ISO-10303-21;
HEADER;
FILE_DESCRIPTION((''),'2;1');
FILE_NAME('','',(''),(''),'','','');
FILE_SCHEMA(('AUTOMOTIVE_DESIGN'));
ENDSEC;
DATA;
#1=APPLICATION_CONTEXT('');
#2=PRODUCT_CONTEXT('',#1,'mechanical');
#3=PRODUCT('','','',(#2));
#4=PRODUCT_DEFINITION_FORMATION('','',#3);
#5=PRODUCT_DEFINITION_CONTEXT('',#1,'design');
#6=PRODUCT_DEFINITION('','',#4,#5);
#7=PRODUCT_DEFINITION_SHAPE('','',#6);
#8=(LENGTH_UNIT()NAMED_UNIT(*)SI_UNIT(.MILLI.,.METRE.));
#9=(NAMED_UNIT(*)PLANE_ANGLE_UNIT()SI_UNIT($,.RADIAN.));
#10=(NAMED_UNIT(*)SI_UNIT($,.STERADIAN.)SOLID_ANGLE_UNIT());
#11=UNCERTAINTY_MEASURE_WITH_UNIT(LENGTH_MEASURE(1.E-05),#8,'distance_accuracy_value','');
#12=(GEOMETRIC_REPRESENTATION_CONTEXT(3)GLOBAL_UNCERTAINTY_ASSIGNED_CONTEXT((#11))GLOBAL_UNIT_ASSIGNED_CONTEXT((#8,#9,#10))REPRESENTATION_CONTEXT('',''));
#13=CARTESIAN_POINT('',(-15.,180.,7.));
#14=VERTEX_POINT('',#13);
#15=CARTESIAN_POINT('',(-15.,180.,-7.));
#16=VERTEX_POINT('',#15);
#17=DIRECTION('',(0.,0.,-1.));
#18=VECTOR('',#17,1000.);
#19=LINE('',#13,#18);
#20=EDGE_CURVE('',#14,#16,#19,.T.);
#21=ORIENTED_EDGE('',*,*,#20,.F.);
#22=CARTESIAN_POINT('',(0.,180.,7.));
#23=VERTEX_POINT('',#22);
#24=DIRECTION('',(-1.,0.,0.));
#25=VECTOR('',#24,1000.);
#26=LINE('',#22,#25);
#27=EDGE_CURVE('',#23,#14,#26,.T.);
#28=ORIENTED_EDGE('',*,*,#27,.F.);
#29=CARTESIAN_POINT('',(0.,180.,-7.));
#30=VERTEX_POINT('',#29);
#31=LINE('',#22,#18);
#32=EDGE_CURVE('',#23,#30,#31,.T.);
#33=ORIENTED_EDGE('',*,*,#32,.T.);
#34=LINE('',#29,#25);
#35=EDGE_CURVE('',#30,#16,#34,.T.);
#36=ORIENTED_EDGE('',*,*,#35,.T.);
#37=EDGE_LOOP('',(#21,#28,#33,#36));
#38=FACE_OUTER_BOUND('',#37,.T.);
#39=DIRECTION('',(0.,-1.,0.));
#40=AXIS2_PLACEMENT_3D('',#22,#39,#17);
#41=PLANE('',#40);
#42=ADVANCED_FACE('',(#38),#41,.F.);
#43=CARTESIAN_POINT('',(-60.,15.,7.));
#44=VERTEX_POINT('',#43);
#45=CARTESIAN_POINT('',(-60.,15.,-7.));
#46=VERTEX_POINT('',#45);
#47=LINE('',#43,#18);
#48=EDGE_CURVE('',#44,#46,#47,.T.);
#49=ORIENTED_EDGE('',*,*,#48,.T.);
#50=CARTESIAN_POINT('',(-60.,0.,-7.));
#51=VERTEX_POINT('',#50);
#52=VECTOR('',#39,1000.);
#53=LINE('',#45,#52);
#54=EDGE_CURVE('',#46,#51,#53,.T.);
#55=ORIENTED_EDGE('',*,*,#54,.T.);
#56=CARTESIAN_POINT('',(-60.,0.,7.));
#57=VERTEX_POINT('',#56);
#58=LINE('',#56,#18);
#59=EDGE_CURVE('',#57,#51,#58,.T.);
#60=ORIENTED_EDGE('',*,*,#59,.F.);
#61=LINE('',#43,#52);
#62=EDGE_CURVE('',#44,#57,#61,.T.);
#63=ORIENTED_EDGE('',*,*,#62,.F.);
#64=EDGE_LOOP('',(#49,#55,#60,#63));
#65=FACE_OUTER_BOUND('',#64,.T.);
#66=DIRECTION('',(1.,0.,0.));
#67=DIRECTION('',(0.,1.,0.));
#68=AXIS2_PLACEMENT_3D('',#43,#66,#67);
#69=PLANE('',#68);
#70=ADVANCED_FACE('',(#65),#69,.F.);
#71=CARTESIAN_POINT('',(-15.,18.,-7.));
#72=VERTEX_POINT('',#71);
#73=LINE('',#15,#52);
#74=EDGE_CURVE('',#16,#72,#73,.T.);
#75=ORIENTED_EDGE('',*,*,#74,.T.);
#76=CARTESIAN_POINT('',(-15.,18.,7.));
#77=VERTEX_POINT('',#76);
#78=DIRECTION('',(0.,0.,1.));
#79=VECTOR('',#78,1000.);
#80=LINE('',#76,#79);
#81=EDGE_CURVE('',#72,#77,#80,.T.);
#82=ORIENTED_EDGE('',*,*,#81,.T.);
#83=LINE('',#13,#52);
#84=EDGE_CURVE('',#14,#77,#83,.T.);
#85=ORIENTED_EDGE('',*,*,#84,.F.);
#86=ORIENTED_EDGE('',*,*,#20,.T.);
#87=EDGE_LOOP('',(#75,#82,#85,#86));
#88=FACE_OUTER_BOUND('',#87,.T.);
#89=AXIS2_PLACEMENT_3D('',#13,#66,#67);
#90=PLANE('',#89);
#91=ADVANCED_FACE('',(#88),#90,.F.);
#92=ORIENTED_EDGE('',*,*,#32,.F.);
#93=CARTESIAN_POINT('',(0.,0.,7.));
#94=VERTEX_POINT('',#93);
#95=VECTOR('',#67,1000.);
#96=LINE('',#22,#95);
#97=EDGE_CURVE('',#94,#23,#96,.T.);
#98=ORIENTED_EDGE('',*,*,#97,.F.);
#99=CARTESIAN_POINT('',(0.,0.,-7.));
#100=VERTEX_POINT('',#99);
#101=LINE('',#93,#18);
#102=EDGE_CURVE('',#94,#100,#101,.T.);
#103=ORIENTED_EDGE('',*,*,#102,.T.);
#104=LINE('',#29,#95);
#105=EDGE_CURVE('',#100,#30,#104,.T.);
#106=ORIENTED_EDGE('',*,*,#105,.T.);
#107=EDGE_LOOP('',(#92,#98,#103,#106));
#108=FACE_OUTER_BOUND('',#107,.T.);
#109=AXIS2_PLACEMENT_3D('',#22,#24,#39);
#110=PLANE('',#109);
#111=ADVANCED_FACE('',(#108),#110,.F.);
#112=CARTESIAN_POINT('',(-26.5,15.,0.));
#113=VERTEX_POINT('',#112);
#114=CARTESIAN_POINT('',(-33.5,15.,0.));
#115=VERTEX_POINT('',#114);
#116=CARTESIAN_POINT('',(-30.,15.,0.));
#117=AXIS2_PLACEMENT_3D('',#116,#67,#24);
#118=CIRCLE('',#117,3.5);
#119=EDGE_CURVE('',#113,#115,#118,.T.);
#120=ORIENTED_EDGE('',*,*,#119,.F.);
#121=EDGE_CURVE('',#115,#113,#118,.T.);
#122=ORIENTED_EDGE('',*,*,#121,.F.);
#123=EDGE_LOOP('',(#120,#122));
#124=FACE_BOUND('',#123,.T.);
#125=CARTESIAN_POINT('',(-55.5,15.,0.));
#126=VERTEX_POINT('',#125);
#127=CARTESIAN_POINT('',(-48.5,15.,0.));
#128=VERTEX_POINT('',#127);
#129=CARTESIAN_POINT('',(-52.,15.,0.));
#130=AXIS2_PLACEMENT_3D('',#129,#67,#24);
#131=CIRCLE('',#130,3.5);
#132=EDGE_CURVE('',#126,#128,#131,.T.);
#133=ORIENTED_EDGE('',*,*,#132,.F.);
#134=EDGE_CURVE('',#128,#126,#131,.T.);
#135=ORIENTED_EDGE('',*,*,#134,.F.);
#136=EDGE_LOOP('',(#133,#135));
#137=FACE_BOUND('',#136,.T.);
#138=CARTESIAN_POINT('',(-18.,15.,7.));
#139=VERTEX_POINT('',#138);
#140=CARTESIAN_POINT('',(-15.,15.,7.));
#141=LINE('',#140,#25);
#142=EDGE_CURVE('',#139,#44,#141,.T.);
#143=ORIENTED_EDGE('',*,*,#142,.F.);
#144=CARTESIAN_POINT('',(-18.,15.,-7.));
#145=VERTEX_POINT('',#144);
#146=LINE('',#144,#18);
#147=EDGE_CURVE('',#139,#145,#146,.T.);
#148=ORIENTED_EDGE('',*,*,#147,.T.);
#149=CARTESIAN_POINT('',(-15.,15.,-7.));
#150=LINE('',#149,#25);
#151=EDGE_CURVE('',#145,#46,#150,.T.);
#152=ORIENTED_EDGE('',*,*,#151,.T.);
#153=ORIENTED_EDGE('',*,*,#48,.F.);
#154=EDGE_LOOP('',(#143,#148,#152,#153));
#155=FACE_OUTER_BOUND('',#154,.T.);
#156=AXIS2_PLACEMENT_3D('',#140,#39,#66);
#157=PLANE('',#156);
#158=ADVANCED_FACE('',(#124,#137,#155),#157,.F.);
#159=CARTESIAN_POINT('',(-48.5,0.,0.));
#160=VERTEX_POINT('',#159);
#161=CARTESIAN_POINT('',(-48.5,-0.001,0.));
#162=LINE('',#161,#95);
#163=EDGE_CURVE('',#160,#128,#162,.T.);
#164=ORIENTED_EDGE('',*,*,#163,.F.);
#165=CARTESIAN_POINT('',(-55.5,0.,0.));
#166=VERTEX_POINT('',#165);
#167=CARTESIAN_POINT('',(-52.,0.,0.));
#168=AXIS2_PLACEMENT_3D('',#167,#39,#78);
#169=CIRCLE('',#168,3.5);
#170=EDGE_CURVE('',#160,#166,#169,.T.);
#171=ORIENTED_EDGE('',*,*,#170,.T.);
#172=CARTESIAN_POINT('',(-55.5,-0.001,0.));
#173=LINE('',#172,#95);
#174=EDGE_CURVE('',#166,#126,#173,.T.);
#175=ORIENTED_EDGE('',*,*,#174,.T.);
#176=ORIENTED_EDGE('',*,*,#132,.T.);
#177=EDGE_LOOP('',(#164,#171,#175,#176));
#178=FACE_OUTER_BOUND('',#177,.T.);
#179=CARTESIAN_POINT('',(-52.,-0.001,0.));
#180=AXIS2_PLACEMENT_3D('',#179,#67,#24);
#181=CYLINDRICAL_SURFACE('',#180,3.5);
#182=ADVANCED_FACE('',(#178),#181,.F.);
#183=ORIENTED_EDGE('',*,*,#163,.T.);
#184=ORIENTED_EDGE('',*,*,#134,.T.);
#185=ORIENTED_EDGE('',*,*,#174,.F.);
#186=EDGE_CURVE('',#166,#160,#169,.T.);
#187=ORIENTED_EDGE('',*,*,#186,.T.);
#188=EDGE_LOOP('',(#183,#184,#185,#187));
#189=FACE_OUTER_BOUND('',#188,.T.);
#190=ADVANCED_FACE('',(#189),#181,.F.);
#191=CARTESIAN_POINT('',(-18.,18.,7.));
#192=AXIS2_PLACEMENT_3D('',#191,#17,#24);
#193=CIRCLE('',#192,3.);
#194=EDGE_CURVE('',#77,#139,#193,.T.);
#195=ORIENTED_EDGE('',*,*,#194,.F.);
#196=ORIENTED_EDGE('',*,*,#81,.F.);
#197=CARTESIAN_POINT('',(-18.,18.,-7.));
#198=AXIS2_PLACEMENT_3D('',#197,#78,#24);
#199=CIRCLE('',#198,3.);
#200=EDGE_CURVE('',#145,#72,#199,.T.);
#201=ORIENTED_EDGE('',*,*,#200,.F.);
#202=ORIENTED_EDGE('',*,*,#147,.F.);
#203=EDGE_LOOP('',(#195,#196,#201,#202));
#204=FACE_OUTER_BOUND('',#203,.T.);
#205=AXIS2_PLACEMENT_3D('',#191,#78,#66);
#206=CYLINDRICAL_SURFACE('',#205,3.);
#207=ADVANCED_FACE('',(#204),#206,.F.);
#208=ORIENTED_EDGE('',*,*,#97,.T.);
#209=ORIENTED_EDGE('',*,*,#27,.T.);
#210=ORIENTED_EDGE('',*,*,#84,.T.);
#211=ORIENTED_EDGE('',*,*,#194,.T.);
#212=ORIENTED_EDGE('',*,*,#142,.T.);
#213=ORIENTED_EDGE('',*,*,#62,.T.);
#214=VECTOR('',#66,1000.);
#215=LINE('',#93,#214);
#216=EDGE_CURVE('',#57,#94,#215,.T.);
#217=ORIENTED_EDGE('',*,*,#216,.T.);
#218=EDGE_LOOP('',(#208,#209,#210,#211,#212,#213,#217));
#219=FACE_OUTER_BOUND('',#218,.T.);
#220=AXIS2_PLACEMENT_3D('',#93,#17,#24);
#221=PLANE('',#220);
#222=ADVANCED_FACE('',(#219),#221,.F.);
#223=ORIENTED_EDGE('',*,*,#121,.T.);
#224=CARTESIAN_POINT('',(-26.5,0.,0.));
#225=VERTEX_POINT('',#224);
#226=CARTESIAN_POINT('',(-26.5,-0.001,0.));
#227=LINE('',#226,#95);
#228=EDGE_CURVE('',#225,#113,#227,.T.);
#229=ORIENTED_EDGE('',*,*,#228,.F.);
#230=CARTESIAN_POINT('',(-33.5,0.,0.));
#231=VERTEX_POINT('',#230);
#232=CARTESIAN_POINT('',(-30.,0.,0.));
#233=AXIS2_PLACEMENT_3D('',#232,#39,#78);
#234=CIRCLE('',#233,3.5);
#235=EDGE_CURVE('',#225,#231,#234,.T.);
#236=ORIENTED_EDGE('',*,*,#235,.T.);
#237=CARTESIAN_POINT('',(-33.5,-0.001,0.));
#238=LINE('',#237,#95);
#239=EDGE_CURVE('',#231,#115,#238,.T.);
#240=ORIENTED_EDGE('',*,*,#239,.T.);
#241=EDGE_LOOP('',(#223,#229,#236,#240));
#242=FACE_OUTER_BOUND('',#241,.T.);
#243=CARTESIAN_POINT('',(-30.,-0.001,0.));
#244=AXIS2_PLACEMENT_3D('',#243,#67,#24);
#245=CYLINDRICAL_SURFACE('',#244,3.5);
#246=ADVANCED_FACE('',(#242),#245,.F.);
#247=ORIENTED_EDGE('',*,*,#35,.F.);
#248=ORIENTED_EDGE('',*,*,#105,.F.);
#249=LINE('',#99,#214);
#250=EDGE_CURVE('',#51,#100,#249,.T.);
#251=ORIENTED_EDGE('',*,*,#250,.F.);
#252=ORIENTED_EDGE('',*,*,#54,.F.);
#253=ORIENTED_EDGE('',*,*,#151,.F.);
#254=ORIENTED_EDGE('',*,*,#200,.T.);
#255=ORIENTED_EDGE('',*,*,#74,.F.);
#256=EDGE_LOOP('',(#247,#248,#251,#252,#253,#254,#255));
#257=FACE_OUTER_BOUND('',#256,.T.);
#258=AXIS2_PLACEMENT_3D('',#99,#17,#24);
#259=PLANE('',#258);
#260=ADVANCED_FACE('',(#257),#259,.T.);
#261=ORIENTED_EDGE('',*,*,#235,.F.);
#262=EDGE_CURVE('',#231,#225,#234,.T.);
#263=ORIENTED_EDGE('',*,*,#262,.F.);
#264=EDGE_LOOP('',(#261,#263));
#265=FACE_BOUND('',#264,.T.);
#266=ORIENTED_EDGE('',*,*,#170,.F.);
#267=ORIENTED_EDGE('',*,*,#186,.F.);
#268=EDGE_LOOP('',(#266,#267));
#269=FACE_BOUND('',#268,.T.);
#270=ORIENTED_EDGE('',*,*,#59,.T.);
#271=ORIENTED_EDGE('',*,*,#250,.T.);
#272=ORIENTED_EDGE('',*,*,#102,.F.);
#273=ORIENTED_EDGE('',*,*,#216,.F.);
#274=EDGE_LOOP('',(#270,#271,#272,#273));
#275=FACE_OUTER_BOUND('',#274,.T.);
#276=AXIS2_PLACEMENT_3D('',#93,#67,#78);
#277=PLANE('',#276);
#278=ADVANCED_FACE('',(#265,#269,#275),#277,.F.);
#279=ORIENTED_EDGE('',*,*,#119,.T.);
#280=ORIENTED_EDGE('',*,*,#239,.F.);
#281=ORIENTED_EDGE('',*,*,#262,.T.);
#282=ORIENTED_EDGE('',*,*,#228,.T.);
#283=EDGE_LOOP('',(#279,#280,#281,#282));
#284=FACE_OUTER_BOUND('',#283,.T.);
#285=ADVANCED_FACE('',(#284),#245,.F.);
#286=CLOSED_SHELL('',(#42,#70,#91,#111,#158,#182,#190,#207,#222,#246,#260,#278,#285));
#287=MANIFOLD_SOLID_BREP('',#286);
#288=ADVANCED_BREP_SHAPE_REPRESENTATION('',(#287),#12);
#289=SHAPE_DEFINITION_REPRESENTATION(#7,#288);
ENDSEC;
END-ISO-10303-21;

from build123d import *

# Parameters (mm, degrees)
EXTRUDE_1_DEPTH     = 7
FILLET_1_R          = 3
CUT_EXTRUDE_1_REACH = 177.71
SKETCH_3_R          = 3.5


with BuildPart() as part:
    # 草图1 → 凸台-拉伸1 (new, symmetric)
    with BuildSketch(Plane.XY):
        Polygon((0, 180), (-15, 180), (-15, 15), (-60, 15), (-60, 0), (0, 0), align=None)
    extrude(amount=EXTRUDE_1_DEPTH, both=True)

    # 圆角1
    fillet_1_edges = [part.edges().sort_by_distance(p)[0] for p in [
        (-15, 15, 0),
    ]]
    fillet(fillet_1_edges, radius=FILLET_1_R)

    # 草图3 → 切除-拉伸1 (cut, up to next)
    with BuildSketch(Plane(origin=(0, 15, 0), x_dir=(1, 0, 0), z_dir=(0, 1, 0)), mode=Mode.PRIVATE) as cut_extrude_1_sk1:
        with Locations(Location((-52, 0, 0), (0, 0, 180))):
            Circle(SKETCH_3_R)
    cut_extrude_1_tool1 = extrude(cut_extrude_1_sk1.sketch, amount=-CUT_EXTRUDE_1_REACH, mode=Mode.PRIVATE) & part.part
    # 草图3 → 切除-拉伸1 (cut, up to next)
    with BuildSketch(Plane(origin=(0, 15, 0), x_dir=(1, 0, 0), z_dir=(0, 1, 0)), mode=Mode.PRIVATE) as cut_extrude_1_sk2:
        with Locations(Location((-30, 0, 0), (0, 0, 180))):
            Circle(SKETCH_3_R)
    cut_extrude_1_tool2 = extrude(cut_extrude_1_sk2.sketch, amount=-CUT_EXTRUDE_1_REACH, mode=Mode.PRIVATE) & part.part
    add(cut_extrude_1_tool1.solids().sort_by_distance((-52, 15, 0))[0], mode=Mode.SUBTRACT)
    add(cut_extrude_1_tool2.solids().sort_by_distance((-30, 15, 0))[0], mode=Mode.SUBTRACT)


solid = part.part
